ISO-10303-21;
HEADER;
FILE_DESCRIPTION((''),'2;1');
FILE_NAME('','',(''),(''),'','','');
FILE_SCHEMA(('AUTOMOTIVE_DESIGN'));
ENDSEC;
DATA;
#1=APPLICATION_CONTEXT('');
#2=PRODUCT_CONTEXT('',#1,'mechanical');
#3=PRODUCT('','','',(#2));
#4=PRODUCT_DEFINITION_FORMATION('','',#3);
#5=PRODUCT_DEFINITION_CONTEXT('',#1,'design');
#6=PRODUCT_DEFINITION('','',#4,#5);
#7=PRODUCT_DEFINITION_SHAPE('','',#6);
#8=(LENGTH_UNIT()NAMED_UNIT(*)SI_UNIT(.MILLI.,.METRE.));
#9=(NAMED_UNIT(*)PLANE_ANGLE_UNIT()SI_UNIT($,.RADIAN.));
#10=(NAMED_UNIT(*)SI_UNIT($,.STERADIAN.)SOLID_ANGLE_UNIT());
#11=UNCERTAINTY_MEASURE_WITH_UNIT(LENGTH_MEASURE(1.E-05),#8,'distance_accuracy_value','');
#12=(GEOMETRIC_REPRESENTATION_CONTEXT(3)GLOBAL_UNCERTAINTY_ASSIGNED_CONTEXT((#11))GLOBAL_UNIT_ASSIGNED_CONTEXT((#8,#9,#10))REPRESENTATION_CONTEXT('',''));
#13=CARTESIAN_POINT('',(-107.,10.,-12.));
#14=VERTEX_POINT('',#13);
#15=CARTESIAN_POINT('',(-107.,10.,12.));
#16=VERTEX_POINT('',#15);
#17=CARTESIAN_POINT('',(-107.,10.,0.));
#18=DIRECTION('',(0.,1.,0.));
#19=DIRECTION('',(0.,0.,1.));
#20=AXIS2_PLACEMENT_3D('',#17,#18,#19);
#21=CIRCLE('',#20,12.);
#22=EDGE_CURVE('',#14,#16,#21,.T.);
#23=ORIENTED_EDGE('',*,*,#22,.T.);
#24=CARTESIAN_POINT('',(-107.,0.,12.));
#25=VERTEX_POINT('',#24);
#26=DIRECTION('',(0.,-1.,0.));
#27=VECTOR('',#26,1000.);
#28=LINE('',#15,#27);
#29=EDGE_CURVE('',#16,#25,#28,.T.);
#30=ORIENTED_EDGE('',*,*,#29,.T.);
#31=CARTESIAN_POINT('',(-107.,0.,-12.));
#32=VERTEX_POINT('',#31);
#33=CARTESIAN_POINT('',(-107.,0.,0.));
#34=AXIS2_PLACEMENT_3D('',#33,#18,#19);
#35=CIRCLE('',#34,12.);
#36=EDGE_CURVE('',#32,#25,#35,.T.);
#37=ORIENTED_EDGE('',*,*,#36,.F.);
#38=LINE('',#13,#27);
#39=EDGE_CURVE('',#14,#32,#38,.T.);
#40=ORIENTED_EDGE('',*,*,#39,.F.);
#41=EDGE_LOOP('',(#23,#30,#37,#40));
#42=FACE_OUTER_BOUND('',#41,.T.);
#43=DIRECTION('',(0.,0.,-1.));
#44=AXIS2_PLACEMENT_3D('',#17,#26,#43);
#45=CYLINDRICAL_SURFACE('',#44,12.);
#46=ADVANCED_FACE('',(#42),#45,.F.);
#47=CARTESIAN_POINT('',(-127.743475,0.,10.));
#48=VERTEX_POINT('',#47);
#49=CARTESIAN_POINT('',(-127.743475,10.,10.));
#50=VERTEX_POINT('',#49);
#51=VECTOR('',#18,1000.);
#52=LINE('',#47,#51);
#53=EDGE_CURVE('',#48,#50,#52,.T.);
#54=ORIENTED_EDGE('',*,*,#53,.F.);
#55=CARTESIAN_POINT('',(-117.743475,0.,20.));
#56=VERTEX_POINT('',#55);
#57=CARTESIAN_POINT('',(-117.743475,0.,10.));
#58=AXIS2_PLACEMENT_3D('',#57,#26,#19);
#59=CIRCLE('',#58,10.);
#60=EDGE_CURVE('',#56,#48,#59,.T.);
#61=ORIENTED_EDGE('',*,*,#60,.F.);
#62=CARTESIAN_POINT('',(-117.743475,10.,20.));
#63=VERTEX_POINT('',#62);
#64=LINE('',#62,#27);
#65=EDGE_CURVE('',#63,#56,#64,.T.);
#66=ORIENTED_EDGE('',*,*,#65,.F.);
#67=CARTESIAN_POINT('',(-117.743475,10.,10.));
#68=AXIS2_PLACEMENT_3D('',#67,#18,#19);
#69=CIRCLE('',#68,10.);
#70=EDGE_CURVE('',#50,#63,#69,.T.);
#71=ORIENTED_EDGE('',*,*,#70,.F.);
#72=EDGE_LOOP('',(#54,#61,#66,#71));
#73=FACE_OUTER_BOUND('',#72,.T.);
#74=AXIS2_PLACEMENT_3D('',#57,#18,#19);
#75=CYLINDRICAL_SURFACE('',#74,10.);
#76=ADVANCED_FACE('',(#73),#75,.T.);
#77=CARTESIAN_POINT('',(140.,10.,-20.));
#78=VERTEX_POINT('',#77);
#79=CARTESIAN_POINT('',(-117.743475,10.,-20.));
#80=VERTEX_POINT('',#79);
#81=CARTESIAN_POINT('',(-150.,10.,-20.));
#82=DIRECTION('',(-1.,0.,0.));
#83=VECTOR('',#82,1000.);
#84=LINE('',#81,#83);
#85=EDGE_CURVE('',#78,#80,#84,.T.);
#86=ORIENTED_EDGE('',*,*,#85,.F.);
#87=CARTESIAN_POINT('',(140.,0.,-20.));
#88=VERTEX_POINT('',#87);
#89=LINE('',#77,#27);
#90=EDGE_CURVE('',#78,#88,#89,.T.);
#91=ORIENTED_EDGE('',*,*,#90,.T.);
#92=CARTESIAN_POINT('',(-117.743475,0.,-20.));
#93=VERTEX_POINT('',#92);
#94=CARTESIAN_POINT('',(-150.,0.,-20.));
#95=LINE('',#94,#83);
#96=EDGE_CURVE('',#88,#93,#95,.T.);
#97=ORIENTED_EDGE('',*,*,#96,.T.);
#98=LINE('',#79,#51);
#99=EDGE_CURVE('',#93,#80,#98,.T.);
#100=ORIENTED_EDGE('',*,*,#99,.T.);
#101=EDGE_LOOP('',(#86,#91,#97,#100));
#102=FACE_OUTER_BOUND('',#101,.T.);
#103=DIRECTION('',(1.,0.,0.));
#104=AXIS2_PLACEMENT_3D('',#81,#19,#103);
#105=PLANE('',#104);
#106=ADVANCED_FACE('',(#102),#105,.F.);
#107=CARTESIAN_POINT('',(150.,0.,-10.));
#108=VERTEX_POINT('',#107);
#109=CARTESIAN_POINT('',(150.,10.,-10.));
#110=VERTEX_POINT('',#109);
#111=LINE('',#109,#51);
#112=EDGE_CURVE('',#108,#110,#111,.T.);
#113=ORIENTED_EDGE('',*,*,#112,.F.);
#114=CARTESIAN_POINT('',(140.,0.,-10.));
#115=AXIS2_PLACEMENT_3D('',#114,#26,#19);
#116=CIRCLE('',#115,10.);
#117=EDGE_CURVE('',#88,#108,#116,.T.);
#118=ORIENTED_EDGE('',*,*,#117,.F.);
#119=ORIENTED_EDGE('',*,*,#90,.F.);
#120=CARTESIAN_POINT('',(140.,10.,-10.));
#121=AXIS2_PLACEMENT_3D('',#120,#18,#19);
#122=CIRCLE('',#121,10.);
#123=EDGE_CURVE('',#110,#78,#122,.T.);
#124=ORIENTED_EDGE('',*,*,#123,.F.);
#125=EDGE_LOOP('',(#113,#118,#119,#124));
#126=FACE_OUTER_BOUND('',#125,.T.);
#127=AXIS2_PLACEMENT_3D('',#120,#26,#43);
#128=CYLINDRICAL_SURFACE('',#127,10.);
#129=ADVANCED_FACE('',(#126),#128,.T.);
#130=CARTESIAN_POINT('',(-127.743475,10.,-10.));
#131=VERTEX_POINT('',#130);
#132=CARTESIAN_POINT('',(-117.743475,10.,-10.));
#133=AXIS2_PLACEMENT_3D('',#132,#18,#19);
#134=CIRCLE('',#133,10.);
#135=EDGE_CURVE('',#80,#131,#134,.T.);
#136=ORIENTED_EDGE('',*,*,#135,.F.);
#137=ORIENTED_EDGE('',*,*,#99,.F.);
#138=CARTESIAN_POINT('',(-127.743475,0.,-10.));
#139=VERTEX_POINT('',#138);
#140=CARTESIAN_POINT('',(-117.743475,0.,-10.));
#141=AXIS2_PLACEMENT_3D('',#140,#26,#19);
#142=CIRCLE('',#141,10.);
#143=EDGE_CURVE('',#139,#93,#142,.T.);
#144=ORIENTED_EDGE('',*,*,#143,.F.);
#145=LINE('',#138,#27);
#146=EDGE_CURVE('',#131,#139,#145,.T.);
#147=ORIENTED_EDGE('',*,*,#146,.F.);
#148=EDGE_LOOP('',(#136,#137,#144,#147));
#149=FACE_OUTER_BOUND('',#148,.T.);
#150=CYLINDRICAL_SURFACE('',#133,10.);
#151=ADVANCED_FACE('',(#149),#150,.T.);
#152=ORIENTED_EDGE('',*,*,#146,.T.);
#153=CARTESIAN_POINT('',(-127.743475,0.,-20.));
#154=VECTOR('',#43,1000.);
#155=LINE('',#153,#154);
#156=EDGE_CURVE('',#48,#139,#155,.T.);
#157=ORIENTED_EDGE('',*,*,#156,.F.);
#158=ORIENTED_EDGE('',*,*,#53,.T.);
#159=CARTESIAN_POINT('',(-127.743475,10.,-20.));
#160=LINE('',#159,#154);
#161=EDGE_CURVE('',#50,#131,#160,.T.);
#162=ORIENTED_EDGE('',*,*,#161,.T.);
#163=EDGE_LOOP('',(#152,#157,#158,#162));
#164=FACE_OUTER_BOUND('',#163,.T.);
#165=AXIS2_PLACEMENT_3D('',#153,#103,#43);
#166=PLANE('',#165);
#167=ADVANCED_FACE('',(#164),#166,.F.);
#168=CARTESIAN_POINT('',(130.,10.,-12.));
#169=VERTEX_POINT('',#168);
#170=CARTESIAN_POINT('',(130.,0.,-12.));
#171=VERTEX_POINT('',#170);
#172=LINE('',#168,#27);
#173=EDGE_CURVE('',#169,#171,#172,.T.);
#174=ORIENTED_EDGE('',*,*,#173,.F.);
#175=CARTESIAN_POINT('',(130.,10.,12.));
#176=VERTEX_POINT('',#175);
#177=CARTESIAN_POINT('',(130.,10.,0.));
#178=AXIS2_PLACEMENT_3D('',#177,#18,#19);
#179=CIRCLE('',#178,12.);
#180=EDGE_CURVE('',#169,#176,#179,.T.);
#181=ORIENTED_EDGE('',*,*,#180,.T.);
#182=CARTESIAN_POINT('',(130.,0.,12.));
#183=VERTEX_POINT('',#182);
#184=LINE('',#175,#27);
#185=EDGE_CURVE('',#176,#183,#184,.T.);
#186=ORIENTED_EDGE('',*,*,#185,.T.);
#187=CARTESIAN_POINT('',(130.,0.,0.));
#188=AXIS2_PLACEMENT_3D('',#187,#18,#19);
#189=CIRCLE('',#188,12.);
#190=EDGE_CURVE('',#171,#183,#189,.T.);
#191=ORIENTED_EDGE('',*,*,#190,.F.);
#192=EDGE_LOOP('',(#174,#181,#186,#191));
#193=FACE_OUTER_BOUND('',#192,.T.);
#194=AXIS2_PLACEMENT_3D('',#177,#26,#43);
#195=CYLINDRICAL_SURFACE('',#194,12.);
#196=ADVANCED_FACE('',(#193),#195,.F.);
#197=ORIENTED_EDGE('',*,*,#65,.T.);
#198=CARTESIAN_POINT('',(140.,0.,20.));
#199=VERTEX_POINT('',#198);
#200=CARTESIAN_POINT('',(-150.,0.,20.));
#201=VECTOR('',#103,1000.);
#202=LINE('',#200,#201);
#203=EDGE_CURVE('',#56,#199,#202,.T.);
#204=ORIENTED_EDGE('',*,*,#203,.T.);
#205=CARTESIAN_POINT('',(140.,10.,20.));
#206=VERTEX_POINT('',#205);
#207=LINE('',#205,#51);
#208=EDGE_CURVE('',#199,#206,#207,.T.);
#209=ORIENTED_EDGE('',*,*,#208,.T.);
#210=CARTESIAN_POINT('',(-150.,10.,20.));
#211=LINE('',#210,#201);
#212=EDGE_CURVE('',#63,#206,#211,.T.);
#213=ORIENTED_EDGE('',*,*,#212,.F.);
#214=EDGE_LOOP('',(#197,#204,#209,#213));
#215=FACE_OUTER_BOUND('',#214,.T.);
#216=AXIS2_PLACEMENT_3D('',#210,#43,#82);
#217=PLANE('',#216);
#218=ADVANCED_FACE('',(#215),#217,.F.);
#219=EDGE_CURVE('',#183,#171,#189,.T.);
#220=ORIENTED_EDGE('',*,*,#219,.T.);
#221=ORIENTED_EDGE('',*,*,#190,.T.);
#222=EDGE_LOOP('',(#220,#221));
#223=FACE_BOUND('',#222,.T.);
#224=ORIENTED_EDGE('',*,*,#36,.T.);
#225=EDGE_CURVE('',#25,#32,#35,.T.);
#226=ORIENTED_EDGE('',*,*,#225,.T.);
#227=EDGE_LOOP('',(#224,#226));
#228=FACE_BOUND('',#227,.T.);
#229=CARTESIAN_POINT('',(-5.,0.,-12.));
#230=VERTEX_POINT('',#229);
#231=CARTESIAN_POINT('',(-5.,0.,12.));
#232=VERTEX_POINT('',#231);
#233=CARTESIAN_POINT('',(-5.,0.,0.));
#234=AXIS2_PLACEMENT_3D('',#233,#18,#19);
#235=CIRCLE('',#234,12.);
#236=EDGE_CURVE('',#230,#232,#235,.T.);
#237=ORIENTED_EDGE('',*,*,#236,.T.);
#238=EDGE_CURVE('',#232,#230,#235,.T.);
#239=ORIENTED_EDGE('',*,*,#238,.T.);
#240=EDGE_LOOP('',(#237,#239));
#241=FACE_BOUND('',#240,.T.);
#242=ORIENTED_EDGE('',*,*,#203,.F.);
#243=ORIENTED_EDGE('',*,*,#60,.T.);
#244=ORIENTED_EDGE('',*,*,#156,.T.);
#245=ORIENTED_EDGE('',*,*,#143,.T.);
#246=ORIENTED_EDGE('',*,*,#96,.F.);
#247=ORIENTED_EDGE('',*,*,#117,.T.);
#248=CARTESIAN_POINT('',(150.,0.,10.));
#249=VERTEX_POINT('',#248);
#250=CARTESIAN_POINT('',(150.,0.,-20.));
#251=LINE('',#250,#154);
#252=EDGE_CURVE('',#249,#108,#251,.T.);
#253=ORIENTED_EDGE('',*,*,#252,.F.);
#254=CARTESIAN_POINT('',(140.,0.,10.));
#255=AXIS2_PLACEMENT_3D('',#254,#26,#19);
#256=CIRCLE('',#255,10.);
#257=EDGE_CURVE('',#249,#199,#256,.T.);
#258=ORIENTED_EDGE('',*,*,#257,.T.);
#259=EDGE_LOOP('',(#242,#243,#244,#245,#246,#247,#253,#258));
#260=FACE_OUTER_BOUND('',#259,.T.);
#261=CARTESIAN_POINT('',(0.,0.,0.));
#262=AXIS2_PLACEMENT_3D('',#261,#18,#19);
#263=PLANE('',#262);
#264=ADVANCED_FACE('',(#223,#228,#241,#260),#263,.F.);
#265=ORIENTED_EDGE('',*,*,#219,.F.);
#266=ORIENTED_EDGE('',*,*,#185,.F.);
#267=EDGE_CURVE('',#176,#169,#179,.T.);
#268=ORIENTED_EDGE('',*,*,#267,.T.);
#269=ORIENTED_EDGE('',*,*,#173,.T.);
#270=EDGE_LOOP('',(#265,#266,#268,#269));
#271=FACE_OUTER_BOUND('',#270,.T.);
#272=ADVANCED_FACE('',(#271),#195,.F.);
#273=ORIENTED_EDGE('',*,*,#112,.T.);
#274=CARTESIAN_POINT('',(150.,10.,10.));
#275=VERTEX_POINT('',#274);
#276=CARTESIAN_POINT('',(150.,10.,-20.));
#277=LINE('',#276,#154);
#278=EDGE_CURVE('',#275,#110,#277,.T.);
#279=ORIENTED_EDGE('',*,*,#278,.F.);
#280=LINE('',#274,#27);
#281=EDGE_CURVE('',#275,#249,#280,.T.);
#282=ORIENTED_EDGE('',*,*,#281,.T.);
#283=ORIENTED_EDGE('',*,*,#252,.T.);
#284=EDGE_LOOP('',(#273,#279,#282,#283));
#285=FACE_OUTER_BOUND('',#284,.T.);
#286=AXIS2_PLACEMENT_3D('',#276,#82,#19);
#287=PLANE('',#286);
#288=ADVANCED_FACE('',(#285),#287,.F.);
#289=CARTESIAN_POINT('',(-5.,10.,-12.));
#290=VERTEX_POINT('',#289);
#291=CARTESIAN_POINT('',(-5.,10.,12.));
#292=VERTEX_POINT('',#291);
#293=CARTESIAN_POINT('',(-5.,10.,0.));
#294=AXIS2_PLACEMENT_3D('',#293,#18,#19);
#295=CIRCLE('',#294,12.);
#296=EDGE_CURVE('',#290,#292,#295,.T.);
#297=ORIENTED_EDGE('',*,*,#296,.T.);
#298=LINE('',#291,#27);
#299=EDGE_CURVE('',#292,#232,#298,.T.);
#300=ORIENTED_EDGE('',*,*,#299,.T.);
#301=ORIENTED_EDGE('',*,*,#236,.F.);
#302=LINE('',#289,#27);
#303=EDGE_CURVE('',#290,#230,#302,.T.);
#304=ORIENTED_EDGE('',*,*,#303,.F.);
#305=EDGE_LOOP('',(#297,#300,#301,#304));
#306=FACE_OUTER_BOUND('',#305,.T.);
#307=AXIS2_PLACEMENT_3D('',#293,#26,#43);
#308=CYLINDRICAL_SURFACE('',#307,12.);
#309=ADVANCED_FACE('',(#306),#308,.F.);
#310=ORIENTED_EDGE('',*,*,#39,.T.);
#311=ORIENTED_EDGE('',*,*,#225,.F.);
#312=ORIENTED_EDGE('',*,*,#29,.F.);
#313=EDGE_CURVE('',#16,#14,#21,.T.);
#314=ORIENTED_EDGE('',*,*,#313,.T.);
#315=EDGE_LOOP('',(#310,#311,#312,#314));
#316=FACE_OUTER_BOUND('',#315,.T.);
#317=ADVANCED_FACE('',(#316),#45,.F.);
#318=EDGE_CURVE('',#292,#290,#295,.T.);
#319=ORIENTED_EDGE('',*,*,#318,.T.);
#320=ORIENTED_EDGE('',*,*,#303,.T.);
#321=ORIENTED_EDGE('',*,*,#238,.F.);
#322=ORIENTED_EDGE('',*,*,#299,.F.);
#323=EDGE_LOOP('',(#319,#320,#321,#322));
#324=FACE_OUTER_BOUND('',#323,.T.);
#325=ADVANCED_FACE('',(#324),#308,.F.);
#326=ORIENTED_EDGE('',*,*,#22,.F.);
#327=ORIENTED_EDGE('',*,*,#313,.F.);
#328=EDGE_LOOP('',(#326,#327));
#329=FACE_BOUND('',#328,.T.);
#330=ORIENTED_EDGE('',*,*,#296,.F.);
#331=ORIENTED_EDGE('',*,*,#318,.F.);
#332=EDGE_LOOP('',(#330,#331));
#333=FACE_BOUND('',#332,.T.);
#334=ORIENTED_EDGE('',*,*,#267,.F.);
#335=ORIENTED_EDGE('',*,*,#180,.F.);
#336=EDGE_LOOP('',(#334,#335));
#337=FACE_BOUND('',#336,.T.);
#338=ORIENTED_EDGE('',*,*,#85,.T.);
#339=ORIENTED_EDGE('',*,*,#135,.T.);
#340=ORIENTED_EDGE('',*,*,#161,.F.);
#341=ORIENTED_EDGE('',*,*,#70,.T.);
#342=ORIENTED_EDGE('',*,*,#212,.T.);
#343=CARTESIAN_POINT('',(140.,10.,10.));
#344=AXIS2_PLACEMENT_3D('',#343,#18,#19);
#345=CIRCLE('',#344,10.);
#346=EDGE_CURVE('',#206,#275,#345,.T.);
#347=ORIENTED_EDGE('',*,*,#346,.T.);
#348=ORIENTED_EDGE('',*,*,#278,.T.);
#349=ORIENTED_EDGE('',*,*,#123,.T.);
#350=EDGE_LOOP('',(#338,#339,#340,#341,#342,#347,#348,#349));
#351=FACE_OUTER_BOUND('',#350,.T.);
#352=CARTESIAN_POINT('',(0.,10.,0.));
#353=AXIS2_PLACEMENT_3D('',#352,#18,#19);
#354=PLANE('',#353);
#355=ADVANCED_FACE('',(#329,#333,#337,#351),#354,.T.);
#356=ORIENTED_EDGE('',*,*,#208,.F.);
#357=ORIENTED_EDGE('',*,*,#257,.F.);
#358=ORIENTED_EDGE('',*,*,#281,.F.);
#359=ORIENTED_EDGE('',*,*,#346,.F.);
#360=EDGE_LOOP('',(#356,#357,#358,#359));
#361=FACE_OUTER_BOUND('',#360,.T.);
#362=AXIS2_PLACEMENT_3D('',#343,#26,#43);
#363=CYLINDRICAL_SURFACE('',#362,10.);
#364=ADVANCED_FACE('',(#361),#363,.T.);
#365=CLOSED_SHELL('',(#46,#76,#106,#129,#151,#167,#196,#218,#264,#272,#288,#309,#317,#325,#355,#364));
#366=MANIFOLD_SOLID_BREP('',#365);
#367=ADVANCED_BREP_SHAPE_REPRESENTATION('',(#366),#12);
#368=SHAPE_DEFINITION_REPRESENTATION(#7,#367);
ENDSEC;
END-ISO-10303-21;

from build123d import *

# Parameters (mm, degrees)
SKETCH1_W           = 300
SKETCH1_H           = 40
SKETCH1_R           = 12
BOSS_EXTRUDE1_DEPTH = 10
SKETCH2_W           = 22.25652502
SKETCH2_H           = 40
CUT_EXTRUDE1_DEPTH  = 10
FILLET1_R           = 10


with BuildPart() as part:
    # Sketch1 → Boss-Extrude1 (new body)
    with BuildSketch(Plane(origin=(0, 0, 0), x_dir=(1, 0, 0), z_dir=(0, 1, 0))):
        Rectangle(SKETCH1_W, SKETCH1_H)
        with Locations(Location((130, 0, 0), (0, 0, 270))):
            Circle(SKETCH1_R, mode=Mode.SUBTRACT)
        with Locations(Location((-5, 0, 0), (0, 0, 270))):
            Circle(SKETCH1_R, mode=Mode.SUBTRACT)
        with Locations(Location((-107, 0, 0), (0, 0, 270))):
            Circle(SKETCH1_R, mode=Mode.SUBTRACT)
    extrude(amount=BOSS_EXTRUDE1_DEPTH)

    # Sketch2 → Cut-Extrude1 (cut)
    with BuildSketch(Plane(origin=(0, 10, 0), x_dir=(1, 0, 0), z_dir=(0, 1, 0))):
        with Locations((-138.87173749, 0)):
            Rectangle(SKETCH2_W, SKETCH2_H)
    extrude(amount=-CUT_EXTRUDE1_DEPTH, mode=Mode.SUBTRACT)

    # Fillet1
    fillet1_edges = [part.edges().sort_by_distance(p)[0] for p in [
        (-127.74347498, 5, -20),
        (-127.74347498, 5, 20),
        (150, 5, 20),
        (150, 5, -20),
    ]]
    fillet(fillet1_edges, radius=FILLET1_R)


solid = part.part
